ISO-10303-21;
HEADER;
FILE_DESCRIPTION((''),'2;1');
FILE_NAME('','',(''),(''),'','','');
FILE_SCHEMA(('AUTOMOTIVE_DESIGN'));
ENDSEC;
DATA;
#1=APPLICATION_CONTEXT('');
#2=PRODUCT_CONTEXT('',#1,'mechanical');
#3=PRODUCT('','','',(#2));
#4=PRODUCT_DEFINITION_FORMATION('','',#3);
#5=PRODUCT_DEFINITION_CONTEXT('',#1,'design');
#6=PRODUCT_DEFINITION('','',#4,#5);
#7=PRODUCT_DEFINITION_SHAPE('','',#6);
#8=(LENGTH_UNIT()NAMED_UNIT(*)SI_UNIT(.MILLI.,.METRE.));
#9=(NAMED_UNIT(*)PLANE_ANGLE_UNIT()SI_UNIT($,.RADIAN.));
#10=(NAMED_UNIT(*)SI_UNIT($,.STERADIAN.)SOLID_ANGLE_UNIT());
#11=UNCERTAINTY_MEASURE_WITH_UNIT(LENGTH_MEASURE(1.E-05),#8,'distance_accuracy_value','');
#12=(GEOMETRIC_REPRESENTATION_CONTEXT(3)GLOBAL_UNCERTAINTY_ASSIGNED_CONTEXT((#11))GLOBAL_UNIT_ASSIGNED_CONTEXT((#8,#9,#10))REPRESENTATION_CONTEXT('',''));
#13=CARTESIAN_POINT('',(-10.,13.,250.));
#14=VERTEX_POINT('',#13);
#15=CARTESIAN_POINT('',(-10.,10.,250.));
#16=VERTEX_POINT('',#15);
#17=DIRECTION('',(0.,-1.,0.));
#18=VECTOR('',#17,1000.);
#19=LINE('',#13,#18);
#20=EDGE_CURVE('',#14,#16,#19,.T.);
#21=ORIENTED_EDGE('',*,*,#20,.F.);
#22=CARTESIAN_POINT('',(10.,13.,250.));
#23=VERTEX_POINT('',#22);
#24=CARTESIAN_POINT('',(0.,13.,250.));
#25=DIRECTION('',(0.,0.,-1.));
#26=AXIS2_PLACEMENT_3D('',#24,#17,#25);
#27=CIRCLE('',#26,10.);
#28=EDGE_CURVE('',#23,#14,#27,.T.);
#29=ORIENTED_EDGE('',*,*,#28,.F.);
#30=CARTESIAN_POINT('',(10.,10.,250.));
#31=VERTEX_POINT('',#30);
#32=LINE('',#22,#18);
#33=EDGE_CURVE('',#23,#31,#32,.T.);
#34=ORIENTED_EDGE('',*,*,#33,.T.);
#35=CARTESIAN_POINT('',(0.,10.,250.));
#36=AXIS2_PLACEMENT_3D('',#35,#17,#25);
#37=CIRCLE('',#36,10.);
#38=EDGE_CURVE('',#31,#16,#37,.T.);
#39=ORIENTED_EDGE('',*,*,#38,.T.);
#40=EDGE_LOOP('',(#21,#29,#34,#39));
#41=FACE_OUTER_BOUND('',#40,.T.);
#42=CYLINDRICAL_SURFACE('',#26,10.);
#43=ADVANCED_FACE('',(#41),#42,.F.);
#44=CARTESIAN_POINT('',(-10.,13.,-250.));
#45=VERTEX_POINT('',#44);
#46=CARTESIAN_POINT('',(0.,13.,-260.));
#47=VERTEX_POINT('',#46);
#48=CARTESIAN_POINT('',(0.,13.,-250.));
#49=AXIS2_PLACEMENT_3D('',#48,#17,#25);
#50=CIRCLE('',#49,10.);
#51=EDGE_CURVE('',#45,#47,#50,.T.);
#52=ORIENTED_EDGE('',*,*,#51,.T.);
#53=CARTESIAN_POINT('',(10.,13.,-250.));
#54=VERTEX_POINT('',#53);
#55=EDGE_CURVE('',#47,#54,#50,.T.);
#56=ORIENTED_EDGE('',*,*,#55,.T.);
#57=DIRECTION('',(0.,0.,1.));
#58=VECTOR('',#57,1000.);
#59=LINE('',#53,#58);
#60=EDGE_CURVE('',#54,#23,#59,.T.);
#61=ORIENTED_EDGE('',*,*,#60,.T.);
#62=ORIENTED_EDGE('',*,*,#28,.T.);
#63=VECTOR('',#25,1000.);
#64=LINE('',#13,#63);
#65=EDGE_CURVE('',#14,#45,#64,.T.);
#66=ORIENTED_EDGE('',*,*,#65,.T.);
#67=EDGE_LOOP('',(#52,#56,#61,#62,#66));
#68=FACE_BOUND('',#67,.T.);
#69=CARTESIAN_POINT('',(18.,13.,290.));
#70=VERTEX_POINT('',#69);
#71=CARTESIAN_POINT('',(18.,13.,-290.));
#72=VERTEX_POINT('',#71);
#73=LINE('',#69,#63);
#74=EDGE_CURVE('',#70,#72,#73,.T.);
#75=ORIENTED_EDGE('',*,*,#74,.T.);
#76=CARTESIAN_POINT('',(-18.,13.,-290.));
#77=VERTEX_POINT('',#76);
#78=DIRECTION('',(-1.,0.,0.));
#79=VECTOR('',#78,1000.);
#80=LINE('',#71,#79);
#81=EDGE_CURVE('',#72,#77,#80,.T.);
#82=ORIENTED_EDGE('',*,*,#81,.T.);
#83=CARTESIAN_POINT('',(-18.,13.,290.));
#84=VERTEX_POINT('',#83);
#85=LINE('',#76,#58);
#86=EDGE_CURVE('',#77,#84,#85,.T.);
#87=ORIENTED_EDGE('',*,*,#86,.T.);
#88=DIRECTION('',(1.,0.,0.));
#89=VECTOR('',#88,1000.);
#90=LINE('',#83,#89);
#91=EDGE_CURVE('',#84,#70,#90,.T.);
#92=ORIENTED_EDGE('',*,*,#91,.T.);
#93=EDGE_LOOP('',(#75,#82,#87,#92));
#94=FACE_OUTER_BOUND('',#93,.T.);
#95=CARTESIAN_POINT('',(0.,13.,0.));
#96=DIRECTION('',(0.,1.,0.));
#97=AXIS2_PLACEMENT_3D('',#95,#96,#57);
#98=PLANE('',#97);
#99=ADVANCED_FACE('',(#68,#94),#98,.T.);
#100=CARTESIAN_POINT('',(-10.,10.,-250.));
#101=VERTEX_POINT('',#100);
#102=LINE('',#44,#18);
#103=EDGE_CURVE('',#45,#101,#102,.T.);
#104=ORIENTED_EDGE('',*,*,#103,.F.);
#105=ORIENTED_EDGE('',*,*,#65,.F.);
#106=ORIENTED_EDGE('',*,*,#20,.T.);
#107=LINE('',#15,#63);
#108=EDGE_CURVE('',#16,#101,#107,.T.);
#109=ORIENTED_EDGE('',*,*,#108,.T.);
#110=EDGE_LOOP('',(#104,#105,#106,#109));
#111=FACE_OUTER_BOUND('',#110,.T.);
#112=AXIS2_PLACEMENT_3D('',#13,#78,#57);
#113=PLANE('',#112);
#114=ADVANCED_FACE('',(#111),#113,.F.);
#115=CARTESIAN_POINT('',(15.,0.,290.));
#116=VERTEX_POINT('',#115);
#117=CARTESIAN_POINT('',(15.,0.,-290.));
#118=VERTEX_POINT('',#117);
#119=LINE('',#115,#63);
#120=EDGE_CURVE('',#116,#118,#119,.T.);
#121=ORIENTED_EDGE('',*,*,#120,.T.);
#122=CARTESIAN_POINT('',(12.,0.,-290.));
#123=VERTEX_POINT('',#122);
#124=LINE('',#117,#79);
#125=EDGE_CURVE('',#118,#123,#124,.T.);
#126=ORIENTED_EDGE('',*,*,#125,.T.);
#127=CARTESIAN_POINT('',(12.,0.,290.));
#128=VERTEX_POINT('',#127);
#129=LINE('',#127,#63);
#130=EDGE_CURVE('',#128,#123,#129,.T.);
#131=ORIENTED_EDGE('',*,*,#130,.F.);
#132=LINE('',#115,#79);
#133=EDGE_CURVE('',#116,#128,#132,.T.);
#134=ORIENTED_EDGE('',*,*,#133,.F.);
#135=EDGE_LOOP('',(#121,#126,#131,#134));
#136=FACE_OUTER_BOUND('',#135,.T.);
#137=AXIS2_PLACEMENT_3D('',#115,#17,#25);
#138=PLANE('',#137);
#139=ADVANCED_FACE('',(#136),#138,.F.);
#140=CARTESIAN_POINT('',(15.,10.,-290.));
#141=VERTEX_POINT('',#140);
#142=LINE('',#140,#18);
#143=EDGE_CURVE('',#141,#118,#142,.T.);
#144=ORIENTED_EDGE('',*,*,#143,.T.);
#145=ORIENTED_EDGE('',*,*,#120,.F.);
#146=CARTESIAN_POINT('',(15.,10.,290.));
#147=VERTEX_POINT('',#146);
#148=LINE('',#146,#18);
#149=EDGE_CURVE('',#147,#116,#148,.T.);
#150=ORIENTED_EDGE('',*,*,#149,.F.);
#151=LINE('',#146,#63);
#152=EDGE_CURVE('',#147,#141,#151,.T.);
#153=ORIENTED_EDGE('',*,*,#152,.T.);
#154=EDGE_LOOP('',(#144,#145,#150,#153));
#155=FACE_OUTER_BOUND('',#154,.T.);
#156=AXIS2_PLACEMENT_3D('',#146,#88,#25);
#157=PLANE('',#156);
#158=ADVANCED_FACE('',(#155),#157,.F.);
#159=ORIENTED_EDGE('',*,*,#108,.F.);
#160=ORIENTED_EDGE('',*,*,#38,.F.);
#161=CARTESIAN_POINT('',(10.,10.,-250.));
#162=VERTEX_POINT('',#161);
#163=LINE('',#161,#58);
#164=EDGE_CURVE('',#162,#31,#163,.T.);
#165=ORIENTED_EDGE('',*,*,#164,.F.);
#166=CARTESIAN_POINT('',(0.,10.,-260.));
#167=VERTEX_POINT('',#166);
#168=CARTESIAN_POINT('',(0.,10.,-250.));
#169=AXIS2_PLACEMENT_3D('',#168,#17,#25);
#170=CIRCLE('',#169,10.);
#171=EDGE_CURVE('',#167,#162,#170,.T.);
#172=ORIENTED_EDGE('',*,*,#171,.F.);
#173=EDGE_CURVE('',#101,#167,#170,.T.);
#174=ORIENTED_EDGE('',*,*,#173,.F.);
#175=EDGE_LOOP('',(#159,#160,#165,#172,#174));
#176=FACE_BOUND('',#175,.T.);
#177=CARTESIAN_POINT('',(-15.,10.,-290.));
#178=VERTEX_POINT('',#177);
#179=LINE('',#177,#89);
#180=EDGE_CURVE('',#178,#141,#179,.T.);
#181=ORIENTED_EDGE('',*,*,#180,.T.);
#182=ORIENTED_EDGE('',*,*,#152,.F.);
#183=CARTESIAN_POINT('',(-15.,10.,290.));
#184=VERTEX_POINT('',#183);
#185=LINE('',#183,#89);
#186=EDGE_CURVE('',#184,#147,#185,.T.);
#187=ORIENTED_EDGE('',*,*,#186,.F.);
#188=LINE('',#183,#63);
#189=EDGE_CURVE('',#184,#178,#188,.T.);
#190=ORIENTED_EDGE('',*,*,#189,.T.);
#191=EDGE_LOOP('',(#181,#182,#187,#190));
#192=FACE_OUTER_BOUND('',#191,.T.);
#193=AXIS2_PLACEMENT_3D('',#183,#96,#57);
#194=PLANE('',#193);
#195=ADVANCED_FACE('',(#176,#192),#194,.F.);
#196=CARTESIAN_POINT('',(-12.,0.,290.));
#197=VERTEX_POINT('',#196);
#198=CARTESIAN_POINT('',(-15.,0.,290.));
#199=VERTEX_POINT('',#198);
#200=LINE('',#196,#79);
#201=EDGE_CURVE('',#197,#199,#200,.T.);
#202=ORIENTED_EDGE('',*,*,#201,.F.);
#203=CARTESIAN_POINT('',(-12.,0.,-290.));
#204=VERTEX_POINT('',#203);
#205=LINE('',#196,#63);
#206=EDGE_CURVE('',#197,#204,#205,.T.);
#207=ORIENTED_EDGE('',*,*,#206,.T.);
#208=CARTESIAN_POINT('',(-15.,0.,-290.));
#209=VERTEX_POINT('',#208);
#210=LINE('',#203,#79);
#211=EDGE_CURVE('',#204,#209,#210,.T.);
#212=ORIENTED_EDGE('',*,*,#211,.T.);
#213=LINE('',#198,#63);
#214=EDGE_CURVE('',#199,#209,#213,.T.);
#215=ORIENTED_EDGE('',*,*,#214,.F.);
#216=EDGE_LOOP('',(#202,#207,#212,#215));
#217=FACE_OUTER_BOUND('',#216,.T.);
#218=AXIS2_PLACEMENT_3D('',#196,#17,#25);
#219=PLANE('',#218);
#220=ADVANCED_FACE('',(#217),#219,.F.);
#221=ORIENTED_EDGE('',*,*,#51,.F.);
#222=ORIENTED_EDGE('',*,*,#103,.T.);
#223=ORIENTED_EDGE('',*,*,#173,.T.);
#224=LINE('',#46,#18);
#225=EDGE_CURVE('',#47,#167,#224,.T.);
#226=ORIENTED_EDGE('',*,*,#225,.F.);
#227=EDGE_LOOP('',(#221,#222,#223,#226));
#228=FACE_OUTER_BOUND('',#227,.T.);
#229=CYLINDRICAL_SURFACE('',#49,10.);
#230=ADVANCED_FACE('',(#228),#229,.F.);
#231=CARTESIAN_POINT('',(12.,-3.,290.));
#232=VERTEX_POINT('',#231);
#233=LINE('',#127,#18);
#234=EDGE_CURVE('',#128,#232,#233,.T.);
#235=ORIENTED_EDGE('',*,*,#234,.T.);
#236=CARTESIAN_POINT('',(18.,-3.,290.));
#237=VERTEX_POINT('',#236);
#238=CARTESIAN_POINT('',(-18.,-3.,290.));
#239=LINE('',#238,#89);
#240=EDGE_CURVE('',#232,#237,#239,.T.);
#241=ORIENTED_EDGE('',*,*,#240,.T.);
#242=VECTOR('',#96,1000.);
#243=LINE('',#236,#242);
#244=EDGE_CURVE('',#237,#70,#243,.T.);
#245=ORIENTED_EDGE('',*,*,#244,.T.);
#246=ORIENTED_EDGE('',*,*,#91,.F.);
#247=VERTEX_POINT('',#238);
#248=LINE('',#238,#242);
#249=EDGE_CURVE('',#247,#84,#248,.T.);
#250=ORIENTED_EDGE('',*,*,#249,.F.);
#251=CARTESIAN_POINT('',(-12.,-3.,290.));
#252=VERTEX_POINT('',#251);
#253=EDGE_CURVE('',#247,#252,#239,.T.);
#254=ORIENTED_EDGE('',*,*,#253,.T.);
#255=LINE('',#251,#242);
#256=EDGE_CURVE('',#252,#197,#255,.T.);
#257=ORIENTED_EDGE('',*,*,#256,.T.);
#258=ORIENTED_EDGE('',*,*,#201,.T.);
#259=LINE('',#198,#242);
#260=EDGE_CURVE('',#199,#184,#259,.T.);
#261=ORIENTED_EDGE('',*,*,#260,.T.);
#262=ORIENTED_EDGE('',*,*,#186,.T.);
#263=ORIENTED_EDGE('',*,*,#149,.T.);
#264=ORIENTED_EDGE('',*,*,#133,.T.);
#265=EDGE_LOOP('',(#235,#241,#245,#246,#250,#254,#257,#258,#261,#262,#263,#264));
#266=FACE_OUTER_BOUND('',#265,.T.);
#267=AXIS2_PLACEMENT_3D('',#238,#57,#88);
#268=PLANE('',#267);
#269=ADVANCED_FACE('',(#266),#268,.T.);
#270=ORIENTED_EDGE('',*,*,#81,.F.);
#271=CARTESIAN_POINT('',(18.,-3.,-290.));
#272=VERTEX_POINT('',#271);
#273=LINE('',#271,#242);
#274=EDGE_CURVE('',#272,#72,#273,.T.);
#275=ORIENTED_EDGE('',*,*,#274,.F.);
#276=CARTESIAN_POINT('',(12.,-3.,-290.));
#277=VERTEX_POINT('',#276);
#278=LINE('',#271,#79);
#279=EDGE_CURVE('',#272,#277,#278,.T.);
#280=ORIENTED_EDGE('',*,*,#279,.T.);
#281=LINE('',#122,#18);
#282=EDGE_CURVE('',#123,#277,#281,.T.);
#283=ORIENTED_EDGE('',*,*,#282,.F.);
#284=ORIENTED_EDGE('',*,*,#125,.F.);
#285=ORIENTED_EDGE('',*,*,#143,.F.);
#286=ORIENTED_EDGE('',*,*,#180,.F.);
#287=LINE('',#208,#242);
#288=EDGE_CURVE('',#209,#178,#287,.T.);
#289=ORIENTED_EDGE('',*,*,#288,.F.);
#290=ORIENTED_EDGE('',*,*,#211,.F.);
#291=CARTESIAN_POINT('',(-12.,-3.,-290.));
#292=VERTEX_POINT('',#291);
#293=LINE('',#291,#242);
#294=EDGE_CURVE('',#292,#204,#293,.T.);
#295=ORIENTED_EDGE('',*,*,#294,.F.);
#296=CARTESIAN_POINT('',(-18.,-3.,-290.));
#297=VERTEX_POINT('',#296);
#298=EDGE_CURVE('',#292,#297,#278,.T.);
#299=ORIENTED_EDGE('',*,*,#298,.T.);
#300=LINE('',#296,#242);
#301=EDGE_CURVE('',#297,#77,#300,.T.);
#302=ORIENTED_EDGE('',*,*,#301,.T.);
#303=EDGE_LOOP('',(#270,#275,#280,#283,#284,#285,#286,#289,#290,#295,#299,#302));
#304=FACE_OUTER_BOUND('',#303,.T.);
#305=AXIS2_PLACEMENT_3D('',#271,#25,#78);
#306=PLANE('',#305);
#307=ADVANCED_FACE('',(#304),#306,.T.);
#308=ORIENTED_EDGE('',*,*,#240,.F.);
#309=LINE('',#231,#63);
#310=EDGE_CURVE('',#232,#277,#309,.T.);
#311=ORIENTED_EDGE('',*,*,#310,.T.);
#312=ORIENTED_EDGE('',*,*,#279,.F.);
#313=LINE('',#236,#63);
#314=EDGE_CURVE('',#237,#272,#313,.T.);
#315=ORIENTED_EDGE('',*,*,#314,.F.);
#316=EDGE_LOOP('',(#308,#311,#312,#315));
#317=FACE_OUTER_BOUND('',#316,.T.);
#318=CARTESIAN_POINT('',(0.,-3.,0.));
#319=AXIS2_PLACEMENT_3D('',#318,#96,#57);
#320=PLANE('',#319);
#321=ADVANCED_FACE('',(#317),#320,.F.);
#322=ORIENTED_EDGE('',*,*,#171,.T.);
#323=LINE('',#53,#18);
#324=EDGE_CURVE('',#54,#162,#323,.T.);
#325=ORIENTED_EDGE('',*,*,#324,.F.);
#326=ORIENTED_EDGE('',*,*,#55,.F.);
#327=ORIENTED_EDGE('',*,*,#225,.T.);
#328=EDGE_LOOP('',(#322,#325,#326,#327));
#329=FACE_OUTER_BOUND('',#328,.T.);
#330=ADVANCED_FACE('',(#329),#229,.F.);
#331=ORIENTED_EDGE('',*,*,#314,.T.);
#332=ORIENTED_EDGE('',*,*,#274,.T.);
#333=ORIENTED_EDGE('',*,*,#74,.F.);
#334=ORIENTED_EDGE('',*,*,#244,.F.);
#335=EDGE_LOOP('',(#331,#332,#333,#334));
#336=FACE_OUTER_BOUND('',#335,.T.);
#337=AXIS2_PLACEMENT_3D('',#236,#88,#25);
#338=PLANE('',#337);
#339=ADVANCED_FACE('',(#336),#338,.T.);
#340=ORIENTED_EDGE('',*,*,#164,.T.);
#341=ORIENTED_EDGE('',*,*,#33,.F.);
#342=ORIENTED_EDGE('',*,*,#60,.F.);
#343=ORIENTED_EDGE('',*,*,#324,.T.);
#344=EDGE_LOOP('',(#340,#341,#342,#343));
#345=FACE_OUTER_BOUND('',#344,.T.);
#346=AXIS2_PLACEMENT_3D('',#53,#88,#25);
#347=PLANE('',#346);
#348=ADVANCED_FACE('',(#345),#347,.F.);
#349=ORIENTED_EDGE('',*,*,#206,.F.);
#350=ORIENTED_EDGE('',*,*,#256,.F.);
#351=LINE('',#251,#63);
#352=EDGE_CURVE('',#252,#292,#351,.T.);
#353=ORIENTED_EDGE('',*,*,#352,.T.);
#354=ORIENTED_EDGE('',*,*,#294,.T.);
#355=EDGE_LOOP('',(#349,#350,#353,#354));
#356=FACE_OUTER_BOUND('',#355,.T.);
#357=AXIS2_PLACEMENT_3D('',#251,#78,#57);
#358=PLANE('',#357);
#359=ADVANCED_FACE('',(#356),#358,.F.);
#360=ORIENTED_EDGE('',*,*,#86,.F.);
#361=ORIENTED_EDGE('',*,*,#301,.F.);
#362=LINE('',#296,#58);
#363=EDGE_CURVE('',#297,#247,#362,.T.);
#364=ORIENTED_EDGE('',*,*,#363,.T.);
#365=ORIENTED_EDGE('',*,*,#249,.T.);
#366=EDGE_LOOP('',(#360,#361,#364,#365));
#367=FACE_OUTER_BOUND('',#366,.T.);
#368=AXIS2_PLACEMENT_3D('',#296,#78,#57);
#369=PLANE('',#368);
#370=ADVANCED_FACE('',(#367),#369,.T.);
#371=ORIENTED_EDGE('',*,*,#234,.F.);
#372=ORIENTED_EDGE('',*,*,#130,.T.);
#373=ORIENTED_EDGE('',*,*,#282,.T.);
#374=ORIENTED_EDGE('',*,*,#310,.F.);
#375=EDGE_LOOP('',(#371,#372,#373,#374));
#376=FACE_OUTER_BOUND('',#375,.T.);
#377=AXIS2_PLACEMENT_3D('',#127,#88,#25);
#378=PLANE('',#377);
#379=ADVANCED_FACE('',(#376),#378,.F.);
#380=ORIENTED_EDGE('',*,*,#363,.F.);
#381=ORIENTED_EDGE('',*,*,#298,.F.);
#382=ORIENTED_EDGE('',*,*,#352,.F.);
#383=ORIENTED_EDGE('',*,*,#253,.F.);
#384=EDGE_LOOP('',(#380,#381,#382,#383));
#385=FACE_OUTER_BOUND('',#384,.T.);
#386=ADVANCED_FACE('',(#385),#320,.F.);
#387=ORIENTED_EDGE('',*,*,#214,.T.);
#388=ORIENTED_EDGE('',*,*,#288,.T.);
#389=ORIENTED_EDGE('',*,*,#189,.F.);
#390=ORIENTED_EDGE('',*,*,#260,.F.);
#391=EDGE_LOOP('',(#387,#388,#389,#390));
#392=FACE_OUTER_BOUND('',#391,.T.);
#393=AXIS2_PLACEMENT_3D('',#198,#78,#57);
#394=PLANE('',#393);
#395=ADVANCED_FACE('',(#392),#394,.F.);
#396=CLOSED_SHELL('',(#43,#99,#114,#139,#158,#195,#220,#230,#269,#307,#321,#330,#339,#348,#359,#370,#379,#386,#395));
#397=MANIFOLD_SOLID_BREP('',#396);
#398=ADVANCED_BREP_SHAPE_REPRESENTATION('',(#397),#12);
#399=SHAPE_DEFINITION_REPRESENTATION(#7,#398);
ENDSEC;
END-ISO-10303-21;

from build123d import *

# Parameters (mm, degrees)
SKETCH1_W           = 36
SKETCH1_H           = 580
BOSS_EXTRUDE1_DEPTH = 16
CUT_EXTRUDE1_DEPTH  = 581.424844403
CUT_EXTRUDE2_DEPTH  = 291.848757948


with BuildPart() as part:
    # Sketch1 → Boss-Extrude1 (new body)
    with BuildSketch(Plane(origin=(0, 13, 0), x_dir=(1, 0, 0), z_dir=(0, 1, 0))):
        Rectangle(SKETCH1_W, SKETCH1_H)
    extrude(amount=-BOSS_EXTRUDE1_DEPTH)

    # Sketch2 → Cut-Extrude1 (cut, through all)
    with BuildSketch(Plane(origin=(0, 0, -290), x_dir=(-1, 0, 0), z_dir=(0, 0, -1))):
        Polygon((12, -3), (12, 0), (15, 0), (15, 10), (-15, 10), (-15, 0), (-12, 0), (-12, -3), align=None)
    extrude(amount=-CUT_EXTRUDE1_DEPTH, mode=Mode.SUBTRACT)

    # Sketch3 → Cut-Extrude2 (cut, through all)
    with BuildSketch(Plane.XZ.offset(-10)):
        with BuildLine():
            Line((10, -250), (10, 250))
            ThreePointArc((10, 250), (0, 260), (-10, 250))
            Line((-10, 250), (-10, -250))
            ThreePointArc((-10, -250), (0, -260), (10, -250))
        make_face()
    extrude(amount=-CUT_EXTRUDE2_DEPTH, mode=Mode.SUBTRACT)


solid = part.part
